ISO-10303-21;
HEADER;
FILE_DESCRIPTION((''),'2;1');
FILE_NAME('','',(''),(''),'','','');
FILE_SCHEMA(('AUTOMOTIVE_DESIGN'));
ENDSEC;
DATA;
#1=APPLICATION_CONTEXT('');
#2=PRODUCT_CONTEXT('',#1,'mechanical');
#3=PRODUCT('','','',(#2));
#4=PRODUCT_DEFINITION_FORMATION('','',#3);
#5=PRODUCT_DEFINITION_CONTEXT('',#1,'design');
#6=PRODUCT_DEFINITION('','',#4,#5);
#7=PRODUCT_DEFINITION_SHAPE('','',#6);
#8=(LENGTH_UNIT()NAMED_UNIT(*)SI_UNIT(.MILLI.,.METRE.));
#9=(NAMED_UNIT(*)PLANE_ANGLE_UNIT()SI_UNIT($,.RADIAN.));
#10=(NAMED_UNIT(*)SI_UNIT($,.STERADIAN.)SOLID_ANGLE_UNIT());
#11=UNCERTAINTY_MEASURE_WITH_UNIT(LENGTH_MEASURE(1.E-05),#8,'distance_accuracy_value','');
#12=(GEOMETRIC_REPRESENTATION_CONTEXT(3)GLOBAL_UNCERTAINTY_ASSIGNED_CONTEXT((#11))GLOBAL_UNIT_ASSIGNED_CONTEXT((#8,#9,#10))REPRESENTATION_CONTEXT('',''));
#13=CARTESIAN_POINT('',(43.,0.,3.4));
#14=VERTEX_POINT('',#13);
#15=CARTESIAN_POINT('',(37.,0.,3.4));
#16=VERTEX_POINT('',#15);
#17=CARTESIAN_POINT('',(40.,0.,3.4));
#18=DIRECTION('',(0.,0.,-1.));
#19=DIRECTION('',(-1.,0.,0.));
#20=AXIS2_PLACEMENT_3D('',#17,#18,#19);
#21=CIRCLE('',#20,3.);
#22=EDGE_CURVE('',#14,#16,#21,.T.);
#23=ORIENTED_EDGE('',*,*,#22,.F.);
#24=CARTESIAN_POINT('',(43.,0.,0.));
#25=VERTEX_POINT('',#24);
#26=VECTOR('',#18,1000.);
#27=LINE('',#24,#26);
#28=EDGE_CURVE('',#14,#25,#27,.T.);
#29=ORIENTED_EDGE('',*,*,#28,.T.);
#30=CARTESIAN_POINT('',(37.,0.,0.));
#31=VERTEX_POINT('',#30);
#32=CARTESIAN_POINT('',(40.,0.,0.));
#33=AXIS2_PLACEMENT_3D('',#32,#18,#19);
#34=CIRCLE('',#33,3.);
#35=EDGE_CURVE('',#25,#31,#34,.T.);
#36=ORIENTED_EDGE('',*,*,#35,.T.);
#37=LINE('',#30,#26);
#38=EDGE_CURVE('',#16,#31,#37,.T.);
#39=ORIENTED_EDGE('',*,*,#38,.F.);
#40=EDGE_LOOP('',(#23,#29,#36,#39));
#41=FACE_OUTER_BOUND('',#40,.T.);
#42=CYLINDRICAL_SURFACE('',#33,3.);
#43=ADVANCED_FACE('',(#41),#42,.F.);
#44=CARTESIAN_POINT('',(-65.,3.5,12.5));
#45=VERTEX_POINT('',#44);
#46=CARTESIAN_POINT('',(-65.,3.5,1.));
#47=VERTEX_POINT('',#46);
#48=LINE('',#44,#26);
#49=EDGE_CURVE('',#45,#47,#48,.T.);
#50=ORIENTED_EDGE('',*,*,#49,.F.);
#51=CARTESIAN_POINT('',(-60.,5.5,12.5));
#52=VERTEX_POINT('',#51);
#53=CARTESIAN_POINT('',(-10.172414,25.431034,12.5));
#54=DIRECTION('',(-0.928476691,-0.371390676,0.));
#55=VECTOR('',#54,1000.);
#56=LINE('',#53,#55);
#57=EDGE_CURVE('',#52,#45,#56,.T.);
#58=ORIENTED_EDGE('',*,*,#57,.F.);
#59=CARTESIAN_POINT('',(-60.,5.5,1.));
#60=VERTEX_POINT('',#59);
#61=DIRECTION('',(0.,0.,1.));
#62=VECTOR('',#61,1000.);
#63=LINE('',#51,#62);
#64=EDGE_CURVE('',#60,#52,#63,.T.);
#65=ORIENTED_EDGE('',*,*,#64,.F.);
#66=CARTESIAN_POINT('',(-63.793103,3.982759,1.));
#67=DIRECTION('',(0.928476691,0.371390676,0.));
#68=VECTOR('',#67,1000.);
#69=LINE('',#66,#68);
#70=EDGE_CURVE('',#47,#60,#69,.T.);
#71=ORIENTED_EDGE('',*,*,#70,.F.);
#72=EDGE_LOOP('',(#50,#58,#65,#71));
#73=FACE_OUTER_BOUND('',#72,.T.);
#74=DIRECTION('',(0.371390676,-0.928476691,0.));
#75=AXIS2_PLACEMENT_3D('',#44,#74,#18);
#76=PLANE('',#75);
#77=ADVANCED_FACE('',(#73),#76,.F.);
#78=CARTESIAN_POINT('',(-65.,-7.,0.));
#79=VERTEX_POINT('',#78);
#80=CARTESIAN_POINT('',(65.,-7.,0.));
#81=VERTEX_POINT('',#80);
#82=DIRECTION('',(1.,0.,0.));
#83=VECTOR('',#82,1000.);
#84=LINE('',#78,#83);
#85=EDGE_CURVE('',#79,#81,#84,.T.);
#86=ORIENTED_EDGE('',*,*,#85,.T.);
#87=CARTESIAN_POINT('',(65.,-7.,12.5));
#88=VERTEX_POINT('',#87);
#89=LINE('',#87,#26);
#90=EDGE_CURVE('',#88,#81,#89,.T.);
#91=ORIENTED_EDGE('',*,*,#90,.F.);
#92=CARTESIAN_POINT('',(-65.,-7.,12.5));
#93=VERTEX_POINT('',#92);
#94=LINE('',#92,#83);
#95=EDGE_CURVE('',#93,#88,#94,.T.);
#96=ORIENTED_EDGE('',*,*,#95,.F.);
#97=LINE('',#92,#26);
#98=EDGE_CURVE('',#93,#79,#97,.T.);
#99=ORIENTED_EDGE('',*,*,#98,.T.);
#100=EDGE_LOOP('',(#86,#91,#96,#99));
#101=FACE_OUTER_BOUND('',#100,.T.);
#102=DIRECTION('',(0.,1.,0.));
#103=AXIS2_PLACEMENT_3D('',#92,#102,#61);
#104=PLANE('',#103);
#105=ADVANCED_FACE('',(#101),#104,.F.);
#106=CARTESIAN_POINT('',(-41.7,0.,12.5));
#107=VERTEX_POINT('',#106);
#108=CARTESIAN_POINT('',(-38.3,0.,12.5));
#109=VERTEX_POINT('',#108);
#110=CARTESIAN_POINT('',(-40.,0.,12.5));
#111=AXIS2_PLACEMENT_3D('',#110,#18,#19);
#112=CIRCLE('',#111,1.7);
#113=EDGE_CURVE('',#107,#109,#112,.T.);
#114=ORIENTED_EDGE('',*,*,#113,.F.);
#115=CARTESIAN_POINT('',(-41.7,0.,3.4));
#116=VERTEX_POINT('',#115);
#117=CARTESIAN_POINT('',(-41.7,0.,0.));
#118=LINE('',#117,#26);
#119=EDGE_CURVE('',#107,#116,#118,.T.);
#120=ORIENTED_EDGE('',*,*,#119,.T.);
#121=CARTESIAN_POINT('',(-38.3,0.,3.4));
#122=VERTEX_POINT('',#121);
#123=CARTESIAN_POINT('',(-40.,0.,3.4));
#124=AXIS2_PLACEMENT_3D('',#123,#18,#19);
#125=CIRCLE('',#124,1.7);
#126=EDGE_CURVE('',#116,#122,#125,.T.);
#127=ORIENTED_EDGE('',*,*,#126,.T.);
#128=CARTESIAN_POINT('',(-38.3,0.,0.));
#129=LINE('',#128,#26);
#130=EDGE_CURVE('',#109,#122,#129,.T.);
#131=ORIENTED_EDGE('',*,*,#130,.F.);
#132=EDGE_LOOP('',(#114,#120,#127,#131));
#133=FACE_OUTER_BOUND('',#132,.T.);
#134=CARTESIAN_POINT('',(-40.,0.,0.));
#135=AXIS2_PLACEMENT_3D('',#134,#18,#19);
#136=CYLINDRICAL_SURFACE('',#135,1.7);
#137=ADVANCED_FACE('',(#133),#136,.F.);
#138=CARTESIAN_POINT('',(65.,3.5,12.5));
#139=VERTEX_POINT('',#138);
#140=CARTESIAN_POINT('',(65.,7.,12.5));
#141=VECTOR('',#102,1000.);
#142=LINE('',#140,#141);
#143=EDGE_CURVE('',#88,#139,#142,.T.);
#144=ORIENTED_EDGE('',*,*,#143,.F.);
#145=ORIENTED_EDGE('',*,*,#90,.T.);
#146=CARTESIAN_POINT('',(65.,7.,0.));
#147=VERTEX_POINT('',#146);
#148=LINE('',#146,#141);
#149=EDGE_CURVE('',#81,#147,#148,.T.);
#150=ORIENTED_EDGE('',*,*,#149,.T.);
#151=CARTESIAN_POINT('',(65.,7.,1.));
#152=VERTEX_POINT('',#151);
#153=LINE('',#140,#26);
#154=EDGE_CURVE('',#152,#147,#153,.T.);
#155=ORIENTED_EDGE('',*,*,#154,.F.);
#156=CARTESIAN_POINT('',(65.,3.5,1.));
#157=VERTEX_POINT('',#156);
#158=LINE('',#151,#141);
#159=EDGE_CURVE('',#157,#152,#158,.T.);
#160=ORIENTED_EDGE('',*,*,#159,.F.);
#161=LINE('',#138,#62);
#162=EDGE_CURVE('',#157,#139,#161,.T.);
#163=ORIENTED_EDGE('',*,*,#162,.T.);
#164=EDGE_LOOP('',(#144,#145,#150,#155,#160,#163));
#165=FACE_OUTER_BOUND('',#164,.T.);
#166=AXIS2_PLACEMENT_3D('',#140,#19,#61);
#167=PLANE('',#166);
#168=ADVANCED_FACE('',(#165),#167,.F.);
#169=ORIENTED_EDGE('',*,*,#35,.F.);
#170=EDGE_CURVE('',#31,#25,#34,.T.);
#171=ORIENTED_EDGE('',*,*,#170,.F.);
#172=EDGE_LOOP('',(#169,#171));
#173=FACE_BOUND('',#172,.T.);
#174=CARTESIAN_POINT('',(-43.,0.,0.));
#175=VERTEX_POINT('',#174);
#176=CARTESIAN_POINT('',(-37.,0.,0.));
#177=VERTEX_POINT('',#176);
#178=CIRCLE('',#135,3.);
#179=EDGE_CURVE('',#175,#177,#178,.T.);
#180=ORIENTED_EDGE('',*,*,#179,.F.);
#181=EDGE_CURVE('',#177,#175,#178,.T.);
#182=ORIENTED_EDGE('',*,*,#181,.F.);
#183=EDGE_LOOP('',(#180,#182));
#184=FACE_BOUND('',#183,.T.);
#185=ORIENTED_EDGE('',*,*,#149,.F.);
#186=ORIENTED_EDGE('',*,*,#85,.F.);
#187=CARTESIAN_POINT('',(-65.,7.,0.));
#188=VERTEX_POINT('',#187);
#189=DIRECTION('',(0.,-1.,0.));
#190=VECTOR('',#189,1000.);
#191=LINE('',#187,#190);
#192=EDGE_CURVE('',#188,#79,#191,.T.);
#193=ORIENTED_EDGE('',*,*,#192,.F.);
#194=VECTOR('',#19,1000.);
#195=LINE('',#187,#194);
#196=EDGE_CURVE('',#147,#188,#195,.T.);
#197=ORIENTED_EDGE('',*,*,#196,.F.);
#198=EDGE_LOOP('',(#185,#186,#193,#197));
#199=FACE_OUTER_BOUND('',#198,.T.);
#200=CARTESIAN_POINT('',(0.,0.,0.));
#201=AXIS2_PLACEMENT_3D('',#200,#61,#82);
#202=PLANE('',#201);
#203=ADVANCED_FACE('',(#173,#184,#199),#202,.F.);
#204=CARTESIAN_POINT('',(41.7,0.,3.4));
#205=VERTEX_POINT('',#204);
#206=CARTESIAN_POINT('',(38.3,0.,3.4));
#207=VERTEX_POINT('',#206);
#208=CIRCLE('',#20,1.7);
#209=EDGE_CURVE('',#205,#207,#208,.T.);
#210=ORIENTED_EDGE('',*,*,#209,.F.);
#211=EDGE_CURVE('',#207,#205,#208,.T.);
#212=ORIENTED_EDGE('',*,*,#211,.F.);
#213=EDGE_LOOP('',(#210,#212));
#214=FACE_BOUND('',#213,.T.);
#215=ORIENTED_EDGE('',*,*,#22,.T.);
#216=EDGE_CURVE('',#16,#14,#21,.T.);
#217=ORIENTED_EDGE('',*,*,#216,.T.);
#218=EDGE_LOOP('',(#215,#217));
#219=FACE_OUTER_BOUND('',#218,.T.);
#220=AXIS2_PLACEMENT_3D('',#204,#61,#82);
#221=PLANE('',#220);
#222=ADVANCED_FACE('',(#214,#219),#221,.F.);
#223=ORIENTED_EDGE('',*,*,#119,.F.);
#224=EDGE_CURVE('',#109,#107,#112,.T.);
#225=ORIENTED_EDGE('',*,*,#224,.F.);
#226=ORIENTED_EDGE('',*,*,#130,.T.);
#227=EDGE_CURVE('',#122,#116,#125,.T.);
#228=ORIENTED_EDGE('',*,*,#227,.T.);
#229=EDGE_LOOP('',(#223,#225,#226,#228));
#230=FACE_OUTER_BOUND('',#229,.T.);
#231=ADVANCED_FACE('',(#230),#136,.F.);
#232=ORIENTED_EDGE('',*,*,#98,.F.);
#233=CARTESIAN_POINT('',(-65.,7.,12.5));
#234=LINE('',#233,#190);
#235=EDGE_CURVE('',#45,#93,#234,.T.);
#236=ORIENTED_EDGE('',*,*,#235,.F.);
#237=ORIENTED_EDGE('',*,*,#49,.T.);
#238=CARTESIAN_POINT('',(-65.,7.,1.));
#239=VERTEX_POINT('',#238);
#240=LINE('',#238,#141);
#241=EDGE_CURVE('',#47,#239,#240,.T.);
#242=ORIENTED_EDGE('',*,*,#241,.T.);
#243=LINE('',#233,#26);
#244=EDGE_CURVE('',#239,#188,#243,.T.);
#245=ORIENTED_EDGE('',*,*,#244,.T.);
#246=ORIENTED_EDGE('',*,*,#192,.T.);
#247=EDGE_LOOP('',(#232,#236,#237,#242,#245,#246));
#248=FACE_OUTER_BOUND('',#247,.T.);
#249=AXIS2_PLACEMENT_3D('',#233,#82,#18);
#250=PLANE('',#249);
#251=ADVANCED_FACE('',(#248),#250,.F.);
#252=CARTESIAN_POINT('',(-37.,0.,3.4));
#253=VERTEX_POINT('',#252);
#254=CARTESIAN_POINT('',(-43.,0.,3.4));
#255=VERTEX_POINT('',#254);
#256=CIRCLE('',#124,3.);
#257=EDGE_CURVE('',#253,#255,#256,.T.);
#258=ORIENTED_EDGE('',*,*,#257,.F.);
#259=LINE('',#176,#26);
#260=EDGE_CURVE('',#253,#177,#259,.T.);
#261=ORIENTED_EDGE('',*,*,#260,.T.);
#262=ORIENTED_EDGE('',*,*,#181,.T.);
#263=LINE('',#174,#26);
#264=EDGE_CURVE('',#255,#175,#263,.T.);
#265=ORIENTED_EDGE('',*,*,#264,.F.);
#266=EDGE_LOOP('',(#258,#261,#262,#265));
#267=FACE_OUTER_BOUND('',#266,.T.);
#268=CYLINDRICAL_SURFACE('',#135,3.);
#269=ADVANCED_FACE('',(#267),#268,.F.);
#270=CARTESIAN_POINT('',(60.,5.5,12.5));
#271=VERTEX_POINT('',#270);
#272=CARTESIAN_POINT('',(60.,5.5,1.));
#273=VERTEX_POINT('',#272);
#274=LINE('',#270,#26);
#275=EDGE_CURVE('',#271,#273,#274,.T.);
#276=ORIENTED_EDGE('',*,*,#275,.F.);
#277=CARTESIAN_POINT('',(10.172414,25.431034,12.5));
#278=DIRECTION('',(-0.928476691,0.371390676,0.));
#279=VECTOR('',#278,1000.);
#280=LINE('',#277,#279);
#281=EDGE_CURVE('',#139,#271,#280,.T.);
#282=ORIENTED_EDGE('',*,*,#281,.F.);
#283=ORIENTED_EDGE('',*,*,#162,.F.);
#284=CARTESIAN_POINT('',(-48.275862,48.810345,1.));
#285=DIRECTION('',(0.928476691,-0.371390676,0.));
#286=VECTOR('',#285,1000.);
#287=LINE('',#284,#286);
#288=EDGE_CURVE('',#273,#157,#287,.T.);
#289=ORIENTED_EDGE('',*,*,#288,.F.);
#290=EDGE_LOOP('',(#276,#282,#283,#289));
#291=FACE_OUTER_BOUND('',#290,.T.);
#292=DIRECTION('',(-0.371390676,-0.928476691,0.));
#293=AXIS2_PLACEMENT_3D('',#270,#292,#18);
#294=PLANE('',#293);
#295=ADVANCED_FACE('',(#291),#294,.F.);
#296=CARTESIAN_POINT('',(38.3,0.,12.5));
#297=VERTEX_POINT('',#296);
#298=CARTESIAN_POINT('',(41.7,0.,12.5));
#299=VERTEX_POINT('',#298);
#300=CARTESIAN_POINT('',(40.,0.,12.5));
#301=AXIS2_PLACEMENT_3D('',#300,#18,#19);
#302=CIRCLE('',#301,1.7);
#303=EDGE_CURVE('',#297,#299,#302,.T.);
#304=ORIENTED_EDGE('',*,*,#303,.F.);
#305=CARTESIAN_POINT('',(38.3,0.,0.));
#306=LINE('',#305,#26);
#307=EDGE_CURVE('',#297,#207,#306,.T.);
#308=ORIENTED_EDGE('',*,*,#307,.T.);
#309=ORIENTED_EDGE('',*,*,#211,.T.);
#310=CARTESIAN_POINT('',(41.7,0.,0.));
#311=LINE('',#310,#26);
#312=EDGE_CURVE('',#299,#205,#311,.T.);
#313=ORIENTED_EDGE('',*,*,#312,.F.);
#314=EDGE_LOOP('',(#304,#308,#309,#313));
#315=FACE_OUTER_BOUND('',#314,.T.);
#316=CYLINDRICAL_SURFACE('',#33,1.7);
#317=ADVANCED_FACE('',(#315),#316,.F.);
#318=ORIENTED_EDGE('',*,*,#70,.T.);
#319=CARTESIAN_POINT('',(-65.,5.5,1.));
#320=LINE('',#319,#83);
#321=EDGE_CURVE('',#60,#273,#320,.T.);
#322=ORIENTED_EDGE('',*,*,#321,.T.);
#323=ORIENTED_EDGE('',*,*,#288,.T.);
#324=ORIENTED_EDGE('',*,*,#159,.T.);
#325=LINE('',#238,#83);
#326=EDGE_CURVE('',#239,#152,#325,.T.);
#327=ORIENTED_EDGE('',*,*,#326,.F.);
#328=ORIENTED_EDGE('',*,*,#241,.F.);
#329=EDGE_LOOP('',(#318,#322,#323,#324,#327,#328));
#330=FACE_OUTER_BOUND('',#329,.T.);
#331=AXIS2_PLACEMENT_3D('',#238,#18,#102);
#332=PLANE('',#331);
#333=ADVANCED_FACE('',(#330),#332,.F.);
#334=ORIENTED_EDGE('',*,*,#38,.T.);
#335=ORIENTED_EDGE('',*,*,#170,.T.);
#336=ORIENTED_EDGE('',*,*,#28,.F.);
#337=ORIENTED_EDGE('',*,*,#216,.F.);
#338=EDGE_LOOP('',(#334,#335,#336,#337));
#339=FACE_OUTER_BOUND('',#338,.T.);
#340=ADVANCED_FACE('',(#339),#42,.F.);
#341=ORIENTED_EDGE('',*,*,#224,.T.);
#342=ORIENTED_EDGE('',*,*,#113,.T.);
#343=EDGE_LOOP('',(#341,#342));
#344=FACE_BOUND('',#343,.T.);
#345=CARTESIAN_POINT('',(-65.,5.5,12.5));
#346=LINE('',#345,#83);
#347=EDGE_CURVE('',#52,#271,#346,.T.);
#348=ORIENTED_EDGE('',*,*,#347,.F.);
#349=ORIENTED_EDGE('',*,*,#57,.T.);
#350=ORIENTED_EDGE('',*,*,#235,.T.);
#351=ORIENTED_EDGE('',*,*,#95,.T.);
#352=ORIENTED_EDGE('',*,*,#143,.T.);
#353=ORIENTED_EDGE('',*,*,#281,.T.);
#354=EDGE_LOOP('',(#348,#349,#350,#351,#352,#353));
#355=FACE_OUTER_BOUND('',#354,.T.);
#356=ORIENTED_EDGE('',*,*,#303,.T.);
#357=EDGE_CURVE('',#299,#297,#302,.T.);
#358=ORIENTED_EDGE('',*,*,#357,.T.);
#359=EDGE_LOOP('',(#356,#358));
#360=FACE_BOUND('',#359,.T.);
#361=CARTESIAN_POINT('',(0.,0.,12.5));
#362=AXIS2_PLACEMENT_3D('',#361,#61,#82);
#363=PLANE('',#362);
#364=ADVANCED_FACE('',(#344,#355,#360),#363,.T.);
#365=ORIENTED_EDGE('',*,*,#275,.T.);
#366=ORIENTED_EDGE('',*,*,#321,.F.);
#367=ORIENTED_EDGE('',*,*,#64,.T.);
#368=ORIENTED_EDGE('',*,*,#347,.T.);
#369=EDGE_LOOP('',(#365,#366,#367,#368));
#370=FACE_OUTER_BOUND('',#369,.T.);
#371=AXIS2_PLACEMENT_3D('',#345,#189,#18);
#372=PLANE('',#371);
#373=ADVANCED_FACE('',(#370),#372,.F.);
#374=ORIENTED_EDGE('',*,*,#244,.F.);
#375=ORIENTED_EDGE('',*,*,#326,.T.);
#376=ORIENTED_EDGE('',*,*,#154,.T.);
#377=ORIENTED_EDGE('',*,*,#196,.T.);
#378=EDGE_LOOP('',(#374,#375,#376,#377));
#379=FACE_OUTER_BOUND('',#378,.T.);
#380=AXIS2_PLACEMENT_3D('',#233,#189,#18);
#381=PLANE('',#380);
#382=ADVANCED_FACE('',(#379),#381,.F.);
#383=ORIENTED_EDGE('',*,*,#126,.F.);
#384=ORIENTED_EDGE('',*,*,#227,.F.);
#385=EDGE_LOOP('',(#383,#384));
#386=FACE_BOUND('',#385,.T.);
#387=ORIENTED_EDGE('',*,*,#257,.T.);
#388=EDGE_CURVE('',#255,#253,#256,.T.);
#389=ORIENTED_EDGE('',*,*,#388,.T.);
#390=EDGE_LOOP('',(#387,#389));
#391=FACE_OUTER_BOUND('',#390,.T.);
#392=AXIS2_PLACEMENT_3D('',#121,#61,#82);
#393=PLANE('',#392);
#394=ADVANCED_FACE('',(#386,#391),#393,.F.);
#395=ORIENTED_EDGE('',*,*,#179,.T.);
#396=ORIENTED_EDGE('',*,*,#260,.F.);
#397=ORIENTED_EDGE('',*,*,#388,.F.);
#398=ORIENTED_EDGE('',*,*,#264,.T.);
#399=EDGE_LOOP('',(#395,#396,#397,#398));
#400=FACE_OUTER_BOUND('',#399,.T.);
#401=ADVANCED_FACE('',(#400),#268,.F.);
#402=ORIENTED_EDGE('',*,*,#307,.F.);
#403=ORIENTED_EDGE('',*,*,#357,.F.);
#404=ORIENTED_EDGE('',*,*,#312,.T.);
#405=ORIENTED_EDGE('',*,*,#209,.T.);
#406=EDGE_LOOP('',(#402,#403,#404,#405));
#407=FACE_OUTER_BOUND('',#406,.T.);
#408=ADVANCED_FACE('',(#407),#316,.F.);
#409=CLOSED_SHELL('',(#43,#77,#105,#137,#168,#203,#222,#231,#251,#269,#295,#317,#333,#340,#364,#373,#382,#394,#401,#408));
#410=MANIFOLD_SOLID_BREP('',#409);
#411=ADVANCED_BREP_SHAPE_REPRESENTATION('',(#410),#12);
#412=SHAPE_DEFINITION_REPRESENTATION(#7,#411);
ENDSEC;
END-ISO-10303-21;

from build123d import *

# Parameters (mm, degrees)
SKETCH_1_W                = 130
SKETCH_1_H                = 14
EXTRUDE_1_DEPTH           = 12.5
SKETCH_2_W                = 11.5
SKETCH_2_H                = 1.5
CUT_EXTRUDE_1_DEPTH       = 131.787040642
CHAMFER_3_SIZE            = 2
CHAMFER_3_SIZE2           = 5
CHAMFER_4_SIZE            = 5
CHAMFER_4_SIZE2           = 2
HOLE_WIZARD_1_D           = 3.4
HOLE_WIZARD_1_CBORE_D     = 6
HOLE_WIZARD_1_CBORE_DEPTH = 3.4


with BuildPart() as part:
    # 草图1 → 凸台-拉伸1 (new body)
    with BuildSketch(Plane.XY):
        Rectangle(SKETCH_1_W, SKETCH_1_H)
    extrude(amount=EXTRUDE_1_DEPTH)

    # 草图2 → 切除-拉伸1 (cut, through all)
    with BuildSketch(Plane(origin=(65, 0, 0), x_dir=(0, 0, -1), z_dir=(1, 0, 0))):
        with Locations((-6.75, 6.25)):
            Rectangle(SKETCH_2_W, SKETCH_2_H)
    extrude(amount=-CUT_EXTRUDE_1_DEPTH, mode=Mode.SUBTRACT)

    # 倒角3
    chamfer_3_edges = [part.edges().sort_by_distance(p)[0] for p in [
        (65, 5.5, 6.75),
    ]]
    chamfer_3_side = [part.faces().sort_by_distance(p)[0] for p in [
        (65, -0.683438986, 6.195324881),
    ]]
    chamfer(chamfer_3_edges, length=CHAMFER_3_SIZE, length2=CHAMFER_3_SIZE2, reference=chamfer_3_side[0])

    # 倒角4
    chamfer_4_edges = [part.edges().sort_by_distance(p)[0] for p in [
        (-65, 5.5, 6.75),
    ]]
    chamfer_4_side = [part.faces().sort_by_distance(p)[0] for p in [
        (-2.5, 5.5, 6.75),
    ]]
    chamfer(chamfer_4_edges, length=CHAMFER_4_SIZE, length2=CHAMFER_4_SIZE2, reference=chamfer_4_side[0])

    # 打孔尺寸根据内六角圆柱头螺钉的类型1 (through all)
    with Locations(Plane(origin=(0, 0, 0), x_dir=(-1, 0, 0), z_dir=(0, 0, -1))):
        with Locations((-40, 0), (40, 0)):
            CounterBoreHole(HOLE_WIZARD_1_D / 2, HOLE_WIZARD_1_CBORE_D / 2, HOLE_WIZARD_1_CBORE_DEPTH)


solid = part.part
